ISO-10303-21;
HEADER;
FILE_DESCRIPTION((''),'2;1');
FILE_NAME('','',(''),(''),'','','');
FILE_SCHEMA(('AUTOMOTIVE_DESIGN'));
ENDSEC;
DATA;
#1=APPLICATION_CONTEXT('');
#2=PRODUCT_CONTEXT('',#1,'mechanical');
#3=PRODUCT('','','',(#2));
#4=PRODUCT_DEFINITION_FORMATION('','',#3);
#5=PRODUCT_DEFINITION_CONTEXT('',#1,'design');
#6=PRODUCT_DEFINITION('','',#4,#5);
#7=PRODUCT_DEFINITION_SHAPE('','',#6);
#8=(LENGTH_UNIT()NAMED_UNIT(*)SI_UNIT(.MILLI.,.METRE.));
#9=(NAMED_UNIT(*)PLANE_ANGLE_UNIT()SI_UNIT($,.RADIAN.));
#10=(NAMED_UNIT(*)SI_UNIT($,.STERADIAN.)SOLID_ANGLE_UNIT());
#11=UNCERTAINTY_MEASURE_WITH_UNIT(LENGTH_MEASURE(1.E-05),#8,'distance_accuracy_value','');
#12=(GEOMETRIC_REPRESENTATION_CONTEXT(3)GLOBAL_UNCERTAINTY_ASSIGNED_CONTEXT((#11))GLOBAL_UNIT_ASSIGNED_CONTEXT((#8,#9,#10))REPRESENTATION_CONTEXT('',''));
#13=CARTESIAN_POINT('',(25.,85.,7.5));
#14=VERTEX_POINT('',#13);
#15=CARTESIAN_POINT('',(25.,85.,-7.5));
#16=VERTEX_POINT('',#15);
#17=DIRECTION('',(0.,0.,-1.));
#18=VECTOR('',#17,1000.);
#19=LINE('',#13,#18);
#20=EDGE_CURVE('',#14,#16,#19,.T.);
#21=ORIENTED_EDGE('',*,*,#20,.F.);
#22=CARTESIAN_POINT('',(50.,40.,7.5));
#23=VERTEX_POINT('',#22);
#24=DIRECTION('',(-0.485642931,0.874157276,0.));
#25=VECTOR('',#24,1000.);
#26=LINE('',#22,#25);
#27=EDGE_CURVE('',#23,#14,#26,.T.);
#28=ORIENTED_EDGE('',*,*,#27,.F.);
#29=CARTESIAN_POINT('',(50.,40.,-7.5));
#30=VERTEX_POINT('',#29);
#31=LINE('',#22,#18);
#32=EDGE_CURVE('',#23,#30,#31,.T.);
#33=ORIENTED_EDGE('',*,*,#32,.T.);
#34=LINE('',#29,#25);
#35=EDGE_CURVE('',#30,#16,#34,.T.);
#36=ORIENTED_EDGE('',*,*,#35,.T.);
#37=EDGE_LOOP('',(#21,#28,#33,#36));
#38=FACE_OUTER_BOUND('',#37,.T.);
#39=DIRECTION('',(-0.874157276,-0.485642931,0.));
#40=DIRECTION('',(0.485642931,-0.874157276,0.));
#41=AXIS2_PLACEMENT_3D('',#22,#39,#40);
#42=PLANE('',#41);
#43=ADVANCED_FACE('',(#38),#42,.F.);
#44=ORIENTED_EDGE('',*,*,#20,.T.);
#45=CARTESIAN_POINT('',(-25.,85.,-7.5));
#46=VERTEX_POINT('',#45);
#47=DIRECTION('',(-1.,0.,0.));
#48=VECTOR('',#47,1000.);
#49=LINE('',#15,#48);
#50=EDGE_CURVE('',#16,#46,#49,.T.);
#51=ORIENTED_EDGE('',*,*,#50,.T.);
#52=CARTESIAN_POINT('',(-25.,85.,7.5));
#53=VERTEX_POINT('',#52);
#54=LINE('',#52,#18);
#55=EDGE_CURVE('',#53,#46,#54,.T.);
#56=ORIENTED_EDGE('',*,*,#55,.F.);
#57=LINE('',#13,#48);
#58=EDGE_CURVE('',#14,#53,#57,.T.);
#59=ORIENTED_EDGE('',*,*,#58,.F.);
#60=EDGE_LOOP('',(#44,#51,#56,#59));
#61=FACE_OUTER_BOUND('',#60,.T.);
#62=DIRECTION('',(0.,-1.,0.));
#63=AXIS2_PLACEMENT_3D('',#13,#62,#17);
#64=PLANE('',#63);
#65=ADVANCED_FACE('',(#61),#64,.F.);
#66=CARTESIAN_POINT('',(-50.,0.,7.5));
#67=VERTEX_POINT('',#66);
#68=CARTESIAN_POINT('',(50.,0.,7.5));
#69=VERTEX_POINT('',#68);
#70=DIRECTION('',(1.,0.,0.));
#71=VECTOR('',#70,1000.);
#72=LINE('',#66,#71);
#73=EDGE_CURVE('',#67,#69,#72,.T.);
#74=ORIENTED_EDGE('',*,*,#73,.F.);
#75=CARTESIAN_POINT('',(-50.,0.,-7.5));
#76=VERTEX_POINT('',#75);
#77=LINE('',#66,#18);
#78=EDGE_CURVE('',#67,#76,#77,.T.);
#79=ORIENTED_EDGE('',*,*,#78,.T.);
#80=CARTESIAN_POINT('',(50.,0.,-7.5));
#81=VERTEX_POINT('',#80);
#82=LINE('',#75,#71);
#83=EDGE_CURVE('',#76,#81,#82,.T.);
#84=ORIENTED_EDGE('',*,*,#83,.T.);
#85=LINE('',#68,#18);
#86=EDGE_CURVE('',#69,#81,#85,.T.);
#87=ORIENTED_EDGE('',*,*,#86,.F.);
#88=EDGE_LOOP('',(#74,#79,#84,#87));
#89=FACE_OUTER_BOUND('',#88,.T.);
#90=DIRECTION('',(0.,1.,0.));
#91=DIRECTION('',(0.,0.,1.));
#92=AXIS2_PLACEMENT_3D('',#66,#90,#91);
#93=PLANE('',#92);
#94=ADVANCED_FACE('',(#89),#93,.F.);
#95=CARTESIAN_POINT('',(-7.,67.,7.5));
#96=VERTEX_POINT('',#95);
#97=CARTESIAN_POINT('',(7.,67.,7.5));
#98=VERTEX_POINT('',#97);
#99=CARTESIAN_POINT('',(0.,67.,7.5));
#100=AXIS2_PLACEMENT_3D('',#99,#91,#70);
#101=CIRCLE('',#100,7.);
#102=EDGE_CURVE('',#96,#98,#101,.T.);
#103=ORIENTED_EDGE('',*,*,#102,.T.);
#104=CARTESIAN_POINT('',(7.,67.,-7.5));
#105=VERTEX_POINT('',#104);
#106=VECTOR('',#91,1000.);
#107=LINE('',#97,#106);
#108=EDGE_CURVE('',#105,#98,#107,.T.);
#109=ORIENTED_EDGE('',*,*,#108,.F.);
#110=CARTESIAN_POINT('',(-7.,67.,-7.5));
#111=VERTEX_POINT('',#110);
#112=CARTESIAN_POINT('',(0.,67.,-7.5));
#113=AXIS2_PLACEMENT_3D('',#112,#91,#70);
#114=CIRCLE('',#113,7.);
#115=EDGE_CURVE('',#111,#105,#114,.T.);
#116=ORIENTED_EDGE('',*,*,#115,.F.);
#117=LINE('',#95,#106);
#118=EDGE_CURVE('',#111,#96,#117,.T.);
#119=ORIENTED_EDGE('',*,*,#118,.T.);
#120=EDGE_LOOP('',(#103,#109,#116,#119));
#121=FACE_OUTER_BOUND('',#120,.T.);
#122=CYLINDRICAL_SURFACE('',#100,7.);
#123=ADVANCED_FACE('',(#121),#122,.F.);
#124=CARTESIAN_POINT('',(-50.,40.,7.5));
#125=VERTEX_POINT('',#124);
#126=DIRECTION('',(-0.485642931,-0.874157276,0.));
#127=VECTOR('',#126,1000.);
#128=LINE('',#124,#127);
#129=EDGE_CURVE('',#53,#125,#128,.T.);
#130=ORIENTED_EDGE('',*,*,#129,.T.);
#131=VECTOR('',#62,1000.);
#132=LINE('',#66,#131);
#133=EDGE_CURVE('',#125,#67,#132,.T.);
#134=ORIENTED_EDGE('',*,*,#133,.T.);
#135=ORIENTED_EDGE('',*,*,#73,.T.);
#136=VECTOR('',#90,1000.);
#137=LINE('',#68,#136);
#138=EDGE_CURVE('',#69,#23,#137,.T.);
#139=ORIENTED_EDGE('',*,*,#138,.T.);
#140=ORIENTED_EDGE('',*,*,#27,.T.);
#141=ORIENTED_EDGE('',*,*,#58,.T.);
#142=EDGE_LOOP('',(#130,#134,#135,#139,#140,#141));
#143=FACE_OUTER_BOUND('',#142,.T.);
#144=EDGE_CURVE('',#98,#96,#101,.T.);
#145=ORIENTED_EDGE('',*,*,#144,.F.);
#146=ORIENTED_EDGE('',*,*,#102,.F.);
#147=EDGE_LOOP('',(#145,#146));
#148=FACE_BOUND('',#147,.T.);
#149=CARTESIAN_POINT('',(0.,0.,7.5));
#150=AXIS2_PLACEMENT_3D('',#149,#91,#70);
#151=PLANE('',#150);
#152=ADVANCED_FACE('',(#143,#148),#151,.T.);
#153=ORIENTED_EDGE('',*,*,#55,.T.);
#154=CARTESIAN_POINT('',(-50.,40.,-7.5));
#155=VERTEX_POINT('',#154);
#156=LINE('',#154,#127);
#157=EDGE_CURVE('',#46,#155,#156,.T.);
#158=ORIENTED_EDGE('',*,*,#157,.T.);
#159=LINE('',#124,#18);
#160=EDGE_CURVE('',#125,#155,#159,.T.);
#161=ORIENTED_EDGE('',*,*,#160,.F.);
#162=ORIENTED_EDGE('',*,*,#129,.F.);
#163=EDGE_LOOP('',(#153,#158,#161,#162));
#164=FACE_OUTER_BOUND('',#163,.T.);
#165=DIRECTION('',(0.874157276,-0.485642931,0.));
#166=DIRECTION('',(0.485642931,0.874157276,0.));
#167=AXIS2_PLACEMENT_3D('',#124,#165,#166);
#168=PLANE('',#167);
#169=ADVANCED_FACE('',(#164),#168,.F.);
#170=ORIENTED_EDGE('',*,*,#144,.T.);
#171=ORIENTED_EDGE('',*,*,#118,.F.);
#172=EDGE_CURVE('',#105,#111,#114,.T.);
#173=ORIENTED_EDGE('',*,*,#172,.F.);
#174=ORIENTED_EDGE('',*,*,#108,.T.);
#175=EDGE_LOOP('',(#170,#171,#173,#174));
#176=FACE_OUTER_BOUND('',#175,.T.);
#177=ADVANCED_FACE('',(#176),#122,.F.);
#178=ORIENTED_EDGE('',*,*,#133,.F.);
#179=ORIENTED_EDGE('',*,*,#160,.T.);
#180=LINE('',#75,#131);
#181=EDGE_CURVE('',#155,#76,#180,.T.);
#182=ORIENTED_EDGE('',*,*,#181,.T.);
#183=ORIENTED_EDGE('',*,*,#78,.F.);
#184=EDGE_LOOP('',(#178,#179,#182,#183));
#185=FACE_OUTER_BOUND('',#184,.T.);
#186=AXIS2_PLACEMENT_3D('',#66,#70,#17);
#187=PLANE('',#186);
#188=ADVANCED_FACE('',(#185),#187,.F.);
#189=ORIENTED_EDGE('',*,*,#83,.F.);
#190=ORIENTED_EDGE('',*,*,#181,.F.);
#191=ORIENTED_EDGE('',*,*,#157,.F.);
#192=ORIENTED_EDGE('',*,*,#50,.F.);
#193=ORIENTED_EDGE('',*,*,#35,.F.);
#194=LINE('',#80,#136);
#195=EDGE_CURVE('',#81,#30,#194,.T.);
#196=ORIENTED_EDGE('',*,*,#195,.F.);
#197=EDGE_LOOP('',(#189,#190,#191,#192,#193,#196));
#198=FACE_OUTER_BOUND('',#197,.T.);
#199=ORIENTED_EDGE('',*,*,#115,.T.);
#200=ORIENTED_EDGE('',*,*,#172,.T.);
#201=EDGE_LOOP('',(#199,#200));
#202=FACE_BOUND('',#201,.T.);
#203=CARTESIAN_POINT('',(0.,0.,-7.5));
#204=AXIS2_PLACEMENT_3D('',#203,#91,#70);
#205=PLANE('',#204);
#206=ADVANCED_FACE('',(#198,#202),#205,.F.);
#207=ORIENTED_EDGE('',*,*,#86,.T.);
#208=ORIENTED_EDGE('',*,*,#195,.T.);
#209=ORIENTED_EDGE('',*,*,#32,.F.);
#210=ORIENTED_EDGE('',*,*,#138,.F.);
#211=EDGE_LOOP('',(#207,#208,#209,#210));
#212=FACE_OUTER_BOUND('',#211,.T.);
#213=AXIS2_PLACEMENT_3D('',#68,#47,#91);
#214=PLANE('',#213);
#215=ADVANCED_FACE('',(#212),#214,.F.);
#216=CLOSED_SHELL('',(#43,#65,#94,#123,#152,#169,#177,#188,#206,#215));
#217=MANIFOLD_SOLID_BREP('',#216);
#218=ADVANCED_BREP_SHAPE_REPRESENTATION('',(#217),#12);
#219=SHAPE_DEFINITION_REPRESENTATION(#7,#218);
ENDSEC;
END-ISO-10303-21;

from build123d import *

# Parameters (mm, degrees)
BOSS_EXTRUDE1_DEPTH = 7.5
M16_TAPPED_HOLE1_D  = 14


with BuildPart() as part:
    # Sketch1 → Boss-Extrude1 (new, symmetric)
    with BuildSketch(Plane.XY):
        Polygon((-50, 0), (50, 0), (50, 40), (25, 85), (-25, 85), (-50, 40), align=None)
    extrude(amount=BOSS_EXTRUDE1_DEPTH, both=True)

    # M16 Tapped Hole1 (through all)
    with Locations(Plane(origin=(0, 67, 7.5), x_dir=(1, 0, 0), z_dir=(0, 0, 1))):
        with Locations((0, 0)):
            Hole(M16_TAPPED_HOLE1_D / 2)


solid = part.part
